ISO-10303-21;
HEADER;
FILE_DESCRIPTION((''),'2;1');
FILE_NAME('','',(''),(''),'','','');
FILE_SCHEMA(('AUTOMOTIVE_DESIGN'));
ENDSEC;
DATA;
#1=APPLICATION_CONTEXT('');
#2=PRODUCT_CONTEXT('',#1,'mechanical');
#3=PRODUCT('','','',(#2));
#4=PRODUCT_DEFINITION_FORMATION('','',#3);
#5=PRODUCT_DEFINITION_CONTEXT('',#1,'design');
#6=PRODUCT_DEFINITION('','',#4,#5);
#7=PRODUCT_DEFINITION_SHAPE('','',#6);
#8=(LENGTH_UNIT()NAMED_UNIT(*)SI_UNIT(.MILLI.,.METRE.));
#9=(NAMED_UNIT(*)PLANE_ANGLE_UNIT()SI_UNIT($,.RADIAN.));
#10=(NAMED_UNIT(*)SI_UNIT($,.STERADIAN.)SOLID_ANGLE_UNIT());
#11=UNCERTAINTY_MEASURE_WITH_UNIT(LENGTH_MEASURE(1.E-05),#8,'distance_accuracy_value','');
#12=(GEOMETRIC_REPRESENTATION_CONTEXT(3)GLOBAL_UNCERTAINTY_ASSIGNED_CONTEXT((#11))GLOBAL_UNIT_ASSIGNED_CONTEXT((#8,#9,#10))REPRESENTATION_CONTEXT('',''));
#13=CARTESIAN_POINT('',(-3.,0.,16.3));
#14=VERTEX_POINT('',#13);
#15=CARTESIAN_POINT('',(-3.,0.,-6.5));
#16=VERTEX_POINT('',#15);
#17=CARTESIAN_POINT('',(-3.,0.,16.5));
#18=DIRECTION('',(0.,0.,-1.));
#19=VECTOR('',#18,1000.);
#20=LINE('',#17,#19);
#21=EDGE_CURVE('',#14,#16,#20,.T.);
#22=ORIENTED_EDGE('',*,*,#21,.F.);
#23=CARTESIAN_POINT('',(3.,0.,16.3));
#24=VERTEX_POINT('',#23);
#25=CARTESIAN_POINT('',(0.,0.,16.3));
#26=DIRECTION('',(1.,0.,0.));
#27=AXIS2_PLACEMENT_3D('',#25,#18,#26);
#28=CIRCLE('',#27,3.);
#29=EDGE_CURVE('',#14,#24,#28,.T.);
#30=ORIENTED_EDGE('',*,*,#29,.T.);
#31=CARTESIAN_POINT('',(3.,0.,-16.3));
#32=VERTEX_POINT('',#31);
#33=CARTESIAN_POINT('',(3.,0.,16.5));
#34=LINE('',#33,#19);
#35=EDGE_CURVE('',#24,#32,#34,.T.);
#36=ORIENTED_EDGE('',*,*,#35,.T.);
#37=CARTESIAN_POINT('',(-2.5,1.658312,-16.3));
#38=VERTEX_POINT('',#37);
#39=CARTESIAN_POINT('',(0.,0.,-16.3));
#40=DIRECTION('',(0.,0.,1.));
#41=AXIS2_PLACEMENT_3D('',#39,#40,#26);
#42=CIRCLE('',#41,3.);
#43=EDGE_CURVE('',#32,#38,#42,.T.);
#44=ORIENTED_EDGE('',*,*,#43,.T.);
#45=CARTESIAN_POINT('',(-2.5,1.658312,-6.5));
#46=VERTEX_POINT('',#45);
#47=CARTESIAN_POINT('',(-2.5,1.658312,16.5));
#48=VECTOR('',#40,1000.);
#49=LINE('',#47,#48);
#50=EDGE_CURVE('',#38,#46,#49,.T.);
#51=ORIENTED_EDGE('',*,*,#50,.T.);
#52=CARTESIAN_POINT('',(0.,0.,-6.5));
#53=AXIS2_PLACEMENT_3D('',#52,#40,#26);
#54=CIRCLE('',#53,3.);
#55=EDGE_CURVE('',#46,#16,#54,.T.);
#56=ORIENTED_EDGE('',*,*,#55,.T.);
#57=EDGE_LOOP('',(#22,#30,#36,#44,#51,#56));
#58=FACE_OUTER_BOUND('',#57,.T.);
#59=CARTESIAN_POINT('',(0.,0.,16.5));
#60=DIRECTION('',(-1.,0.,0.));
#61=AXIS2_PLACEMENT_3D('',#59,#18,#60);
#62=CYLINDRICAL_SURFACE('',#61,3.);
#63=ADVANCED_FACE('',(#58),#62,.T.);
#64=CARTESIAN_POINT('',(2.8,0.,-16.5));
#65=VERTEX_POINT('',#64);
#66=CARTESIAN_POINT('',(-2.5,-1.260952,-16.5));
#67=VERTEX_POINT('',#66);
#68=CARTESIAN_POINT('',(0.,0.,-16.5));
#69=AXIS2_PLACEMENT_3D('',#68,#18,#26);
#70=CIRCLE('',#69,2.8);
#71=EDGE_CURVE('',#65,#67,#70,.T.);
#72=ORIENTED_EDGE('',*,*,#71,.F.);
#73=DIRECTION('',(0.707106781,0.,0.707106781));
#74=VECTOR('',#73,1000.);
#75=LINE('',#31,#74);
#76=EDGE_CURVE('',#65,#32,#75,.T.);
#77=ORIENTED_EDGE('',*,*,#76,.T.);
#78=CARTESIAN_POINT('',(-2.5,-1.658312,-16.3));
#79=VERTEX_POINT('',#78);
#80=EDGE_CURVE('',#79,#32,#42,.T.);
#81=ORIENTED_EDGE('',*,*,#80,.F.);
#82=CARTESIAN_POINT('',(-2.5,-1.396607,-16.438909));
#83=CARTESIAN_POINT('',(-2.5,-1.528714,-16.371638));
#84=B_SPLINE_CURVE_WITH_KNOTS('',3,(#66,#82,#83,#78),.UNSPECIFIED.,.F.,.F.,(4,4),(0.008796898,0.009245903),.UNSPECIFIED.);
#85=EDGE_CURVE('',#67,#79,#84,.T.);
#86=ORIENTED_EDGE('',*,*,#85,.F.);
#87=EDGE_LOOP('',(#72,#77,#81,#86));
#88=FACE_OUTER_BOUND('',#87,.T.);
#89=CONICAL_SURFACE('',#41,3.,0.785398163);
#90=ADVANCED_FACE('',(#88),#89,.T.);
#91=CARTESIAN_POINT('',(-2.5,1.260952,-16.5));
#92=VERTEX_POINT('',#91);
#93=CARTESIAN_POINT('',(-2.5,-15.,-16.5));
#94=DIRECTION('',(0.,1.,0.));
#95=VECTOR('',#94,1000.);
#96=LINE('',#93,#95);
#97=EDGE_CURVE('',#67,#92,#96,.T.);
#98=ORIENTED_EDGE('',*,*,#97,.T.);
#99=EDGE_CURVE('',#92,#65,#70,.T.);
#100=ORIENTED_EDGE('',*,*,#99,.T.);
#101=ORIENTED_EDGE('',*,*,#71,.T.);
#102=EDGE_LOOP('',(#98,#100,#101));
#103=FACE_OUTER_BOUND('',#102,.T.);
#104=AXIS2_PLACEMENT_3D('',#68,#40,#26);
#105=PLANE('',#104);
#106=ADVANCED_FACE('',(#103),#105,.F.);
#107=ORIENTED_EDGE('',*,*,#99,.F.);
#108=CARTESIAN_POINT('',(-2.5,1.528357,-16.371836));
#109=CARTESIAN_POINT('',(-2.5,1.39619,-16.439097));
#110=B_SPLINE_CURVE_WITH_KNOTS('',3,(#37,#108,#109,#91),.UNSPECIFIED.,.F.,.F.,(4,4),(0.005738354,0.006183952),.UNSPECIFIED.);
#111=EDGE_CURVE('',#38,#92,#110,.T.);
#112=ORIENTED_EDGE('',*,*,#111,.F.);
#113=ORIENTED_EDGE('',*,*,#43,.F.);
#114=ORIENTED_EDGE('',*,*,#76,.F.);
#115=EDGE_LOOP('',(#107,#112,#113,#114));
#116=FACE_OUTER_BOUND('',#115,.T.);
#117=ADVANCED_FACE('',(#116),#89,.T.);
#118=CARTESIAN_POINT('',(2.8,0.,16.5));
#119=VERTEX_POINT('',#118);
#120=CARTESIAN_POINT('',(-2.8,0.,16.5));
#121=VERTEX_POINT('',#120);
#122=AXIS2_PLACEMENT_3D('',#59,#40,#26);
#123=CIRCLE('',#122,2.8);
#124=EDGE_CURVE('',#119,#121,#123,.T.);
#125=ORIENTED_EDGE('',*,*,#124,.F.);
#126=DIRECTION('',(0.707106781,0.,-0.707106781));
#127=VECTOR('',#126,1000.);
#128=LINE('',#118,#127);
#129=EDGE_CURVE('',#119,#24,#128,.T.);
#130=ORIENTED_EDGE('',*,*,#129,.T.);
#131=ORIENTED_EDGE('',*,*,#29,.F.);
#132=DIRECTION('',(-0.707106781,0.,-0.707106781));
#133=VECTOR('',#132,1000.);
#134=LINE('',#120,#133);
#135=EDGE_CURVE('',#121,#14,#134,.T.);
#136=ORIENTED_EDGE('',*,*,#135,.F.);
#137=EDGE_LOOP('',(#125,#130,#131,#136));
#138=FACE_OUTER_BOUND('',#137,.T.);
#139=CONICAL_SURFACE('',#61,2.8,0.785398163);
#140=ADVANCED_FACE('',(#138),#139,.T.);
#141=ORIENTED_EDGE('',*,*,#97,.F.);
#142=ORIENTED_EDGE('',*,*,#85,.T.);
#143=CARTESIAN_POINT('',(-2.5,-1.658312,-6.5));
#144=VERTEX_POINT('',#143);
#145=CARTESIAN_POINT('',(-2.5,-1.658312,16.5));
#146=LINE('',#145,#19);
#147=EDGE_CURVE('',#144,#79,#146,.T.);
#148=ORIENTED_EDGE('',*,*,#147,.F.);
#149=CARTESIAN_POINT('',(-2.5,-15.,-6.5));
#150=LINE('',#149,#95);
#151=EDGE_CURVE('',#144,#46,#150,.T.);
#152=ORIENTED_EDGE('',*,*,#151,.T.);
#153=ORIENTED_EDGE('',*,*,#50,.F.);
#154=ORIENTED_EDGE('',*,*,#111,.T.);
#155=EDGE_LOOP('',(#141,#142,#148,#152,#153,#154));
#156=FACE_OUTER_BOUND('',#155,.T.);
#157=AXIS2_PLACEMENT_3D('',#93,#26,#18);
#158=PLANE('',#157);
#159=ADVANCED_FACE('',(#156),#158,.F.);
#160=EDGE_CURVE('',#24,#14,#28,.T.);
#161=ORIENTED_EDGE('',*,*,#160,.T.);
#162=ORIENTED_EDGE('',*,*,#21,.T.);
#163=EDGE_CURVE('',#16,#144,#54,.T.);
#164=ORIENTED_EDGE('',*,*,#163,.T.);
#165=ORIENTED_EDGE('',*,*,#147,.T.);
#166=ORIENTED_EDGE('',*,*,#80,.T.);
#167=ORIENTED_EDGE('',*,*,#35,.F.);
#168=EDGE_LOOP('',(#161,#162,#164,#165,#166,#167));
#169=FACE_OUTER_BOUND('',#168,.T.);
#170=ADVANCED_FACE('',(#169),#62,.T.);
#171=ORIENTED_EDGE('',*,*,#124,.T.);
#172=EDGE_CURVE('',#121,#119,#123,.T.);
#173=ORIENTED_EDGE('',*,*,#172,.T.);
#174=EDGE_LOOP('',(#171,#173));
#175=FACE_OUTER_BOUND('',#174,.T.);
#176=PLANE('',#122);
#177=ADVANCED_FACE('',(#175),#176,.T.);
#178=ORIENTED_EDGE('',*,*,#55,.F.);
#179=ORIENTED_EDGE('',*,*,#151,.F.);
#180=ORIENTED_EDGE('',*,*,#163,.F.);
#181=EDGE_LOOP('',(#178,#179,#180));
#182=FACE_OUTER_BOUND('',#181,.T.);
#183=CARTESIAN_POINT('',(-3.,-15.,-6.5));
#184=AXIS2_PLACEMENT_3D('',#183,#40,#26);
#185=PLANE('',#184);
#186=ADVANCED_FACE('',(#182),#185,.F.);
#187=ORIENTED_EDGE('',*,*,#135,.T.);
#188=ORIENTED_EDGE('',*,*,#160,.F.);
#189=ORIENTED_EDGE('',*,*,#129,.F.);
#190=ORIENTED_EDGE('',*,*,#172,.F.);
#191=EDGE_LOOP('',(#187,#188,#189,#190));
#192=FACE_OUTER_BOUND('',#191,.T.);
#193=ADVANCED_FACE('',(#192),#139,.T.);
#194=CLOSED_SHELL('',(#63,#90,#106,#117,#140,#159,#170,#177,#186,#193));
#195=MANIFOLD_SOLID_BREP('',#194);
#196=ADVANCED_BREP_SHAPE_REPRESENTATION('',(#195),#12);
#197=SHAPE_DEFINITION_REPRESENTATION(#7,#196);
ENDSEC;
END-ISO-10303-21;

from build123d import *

# Parameters (mm, degrees)
SKETCH1_R           = 3
BOSS_EXTRUDE1_DEPTH = 16.5
CHAMFER1_SIZE       = 0.2
SKETCH2_W           = 0.5
SKETCH2_H           = 10
CUT_EXTRUDE1_DEPTH  = 15


with BuildPart() as part:
    # Sketch1 → Boss-Extrude1 (new, symmetric)
    with BuildSketch(Plane.XY):
        Circle(SKETCH1_R)
    extrude(amount=BOSS_EXTRUDE1_DEPTH, both=True)

    # Chamfer1
    chamfer1_edges = [part.edges().sort_by_distance(p)[0] for p in [
        (-3, 0, -16.5),
        (-3, 0, 16.5),
    ]]
    chamfer(chamfer1_edges, length=CHAMFER1_SIZE)

    # Sketch2 → Cut-Extrude1 (cut, symmetric)
    with BuildSketch(Plane(origin=(0, 0, 0), x_dir=(1, 0, 0), z_dir=(0, 1, 0))):
        with Locations((-2.75, 11.5)):
            Rectangle(SKETCH2_W, SKETCH2_H)
    extrude(amount=CUT_EXTRUDE1_DEPTH, both=True, mode=Mode.SUBTRACT)


solid = part.part
